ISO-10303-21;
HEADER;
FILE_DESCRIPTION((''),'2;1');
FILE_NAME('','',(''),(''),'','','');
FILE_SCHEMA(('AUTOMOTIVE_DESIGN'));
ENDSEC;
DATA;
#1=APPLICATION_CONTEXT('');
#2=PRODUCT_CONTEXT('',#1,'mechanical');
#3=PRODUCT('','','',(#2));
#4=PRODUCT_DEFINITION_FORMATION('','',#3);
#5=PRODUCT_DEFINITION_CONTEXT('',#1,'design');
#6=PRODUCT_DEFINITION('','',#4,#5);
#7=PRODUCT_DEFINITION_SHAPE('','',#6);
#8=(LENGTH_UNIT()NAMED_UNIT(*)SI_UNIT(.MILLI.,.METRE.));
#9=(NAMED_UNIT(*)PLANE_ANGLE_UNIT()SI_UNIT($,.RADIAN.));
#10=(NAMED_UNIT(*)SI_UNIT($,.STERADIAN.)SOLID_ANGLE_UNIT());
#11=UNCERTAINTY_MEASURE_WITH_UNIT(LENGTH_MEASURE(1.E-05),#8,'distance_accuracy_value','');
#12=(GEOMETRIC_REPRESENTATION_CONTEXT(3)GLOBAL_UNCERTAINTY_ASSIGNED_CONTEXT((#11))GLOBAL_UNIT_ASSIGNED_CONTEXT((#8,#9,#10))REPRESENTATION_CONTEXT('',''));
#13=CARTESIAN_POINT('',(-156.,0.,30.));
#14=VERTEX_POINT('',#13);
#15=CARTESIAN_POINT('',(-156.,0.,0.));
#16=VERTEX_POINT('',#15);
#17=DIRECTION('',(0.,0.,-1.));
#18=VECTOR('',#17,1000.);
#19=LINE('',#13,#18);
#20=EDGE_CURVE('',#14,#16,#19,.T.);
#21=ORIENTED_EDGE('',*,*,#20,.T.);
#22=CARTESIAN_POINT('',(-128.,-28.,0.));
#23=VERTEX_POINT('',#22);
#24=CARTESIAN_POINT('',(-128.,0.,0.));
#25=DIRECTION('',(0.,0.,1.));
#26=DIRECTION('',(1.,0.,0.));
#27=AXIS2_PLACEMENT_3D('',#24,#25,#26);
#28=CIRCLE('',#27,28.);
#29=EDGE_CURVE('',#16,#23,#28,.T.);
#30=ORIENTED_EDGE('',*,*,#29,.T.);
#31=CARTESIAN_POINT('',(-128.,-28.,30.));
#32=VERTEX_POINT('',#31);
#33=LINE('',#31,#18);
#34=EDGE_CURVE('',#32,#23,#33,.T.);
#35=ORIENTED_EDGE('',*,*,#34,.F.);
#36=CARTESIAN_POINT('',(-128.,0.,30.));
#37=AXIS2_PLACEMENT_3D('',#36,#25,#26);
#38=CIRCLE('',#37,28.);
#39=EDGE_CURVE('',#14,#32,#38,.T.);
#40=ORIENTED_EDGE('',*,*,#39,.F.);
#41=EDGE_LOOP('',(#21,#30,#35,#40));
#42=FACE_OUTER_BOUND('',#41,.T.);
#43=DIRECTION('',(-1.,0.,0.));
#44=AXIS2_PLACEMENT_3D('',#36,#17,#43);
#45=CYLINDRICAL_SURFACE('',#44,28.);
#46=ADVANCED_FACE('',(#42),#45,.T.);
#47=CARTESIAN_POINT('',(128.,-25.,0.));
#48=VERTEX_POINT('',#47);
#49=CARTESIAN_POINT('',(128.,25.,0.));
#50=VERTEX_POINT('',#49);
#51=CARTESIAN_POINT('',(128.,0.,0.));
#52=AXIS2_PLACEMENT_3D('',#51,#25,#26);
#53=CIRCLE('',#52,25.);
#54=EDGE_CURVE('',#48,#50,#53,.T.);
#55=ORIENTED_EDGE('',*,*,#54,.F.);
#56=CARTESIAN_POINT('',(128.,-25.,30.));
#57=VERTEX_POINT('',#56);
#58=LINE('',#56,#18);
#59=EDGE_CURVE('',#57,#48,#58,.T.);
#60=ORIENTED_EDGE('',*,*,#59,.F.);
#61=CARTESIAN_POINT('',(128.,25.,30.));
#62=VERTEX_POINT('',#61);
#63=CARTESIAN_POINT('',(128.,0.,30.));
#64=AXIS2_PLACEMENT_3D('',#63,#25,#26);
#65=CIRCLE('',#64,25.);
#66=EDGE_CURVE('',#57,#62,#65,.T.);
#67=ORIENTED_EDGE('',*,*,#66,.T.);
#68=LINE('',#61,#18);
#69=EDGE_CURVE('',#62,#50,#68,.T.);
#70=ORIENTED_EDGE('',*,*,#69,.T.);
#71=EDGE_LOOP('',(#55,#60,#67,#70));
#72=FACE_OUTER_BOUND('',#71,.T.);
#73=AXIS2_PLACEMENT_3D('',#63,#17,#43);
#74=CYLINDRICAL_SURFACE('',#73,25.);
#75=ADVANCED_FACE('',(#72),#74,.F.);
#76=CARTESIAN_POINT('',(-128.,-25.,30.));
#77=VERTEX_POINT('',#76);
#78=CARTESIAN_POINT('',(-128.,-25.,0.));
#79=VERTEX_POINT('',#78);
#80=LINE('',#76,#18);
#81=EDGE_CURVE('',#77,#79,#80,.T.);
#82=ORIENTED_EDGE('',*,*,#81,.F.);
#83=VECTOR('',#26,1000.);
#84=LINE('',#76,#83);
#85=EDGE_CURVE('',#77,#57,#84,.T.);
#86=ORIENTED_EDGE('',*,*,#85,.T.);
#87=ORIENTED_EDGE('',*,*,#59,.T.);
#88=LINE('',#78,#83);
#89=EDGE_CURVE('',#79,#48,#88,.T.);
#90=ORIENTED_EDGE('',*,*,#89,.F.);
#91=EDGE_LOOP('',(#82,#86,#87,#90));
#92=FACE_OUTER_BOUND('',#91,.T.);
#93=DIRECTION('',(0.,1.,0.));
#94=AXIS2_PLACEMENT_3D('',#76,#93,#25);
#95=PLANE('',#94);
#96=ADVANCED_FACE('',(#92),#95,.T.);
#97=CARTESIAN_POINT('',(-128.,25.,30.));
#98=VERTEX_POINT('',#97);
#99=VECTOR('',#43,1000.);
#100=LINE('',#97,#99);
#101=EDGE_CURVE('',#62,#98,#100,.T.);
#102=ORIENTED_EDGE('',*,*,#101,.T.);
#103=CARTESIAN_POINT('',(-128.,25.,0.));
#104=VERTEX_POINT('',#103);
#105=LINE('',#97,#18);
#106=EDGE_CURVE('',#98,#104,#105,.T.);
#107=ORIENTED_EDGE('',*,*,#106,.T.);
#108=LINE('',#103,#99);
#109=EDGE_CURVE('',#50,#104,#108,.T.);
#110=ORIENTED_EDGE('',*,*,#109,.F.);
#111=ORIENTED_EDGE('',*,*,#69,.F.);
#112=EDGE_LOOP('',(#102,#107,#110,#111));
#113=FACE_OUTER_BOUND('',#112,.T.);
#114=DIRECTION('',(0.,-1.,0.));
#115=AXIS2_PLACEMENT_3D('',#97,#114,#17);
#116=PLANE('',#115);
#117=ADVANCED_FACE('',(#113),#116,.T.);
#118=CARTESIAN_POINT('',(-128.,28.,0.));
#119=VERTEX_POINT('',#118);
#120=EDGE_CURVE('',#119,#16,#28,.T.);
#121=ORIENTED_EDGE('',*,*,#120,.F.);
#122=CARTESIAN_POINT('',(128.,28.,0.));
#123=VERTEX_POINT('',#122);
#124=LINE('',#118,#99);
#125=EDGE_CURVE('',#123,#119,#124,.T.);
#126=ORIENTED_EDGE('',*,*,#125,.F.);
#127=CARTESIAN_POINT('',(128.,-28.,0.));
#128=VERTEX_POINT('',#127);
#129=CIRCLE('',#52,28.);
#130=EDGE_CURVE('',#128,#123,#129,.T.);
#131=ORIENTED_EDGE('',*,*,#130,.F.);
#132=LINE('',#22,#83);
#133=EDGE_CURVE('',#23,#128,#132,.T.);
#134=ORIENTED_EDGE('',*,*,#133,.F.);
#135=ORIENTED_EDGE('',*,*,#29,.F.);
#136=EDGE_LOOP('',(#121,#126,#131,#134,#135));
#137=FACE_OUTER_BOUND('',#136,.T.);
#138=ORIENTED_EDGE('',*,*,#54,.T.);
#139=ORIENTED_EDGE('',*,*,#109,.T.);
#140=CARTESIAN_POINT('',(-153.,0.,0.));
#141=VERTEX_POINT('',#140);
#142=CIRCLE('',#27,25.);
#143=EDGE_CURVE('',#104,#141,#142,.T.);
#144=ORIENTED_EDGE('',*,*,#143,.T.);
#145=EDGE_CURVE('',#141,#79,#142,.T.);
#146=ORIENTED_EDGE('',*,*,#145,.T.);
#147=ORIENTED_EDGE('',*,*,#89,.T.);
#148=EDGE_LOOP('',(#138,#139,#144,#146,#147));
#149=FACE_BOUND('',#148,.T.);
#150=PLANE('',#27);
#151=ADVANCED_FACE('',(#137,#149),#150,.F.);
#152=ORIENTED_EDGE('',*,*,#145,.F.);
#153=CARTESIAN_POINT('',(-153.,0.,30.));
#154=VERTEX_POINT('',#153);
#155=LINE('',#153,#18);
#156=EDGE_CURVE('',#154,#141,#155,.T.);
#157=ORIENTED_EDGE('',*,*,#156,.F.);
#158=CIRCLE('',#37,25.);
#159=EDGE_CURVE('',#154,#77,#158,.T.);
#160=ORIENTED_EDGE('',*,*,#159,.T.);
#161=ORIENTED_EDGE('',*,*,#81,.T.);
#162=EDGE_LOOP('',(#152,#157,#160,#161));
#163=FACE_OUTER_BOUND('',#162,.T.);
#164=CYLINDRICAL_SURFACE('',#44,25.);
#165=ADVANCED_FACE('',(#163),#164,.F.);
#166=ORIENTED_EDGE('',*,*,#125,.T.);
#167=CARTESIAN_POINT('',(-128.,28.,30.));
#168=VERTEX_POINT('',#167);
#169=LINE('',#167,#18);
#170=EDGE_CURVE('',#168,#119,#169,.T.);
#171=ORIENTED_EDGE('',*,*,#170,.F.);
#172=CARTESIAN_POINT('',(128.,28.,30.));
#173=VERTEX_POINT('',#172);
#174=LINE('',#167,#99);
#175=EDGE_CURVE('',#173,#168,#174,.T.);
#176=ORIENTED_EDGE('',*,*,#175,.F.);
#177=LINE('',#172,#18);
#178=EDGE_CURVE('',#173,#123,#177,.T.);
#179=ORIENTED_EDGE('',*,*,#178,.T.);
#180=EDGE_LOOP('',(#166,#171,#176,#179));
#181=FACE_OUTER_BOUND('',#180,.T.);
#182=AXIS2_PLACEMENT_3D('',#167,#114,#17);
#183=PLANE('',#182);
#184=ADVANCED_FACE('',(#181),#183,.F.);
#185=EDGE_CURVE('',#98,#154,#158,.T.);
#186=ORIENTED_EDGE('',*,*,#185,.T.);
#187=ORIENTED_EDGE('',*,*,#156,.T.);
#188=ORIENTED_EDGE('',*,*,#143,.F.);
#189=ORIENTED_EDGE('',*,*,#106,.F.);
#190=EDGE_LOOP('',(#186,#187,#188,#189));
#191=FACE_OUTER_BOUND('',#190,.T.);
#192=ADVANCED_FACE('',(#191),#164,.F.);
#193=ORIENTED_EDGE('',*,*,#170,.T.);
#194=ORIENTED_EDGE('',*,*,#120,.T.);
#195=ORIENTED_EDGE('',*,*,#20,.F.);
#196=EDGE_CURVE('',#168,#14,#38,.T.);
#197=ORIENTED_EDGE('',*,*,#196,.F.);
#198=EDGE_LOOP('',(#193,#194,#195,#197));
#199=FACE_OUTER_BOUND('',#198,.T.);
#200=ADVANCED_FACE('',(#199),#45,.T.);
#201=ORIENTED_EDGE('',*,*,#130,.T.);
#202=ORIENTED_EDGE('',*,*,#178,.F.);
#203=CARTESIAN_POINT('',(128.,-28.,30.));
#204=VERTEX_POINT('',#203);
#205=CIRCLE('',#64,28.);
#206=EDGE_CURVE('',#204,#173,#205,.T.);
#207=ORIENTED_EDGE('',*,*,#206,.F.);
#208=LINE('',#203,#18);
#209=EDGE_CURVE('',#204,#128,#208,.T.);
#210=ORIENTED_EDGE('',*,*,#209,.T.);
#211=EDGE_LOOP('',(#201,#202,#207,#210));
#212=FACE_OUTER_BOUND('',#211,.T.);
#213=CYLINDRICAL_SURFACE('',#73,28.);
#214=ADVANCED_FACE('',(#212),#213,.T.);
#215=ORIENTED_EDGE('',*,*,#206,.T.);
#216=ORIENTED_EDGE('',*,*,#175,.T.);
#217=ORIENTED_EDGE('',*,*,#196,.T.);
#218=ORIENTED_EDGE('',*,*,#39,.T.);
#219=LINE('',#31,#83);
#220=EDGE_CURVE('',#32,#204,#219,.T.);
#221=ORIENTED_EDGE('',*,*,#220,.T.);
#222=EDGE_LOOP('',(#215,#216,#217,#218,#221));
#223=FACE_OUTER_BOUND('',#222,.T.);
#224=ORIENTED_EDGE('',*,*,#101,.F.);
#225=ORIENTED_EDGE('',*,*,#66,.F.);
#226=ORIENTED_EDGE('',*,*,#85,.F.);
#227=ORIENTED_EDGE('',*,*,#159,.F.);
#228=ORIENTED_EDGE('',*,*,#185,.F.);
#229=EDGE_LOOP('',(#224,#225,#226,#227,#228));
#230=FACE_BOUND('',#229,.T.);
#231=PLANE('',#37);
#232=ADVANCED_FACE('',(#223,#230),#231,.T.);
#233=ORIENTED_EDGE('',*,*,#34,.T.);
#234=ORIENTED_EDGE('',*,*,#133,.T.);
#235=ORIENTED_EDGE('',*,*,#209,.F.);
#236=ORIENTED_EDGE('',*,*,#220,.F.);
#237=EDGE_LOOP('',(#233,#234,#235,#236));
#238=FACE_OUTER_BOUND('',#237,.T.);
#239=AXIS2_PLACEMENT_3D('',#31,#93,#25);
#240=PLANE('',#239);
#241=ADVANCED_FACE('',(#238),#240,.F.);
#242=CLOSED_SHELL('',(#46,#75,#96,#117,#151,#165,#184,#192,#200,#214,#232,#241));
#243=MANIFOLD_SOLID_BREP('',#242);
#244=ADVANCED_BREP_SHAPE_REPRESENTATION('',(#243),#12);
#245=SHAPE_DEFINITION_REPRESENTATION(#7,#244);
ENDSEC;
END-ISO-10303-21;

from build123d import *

# Parameters (mm, degrees)
EXTRUDE_1_DEPTH = 30


with BuildPart() as part:
    # 草图1 → 拉伸-薄壁1 (new body)
    with BuildSketch(Plane.XY):
        with BuildLine():
            Line((128, -28), (-128, -28))
            ThreePointArc((-128, -28), (-156, 0), (-128, 28))
            Line((-128, 28), (128, 28))
            ThreePointArc((128, 28), (156, 0), (128, -28))
        make_face()
        with BuildLine():
            Line((128, -25), (-128, -25))
            ThreePointArc((-128, -25), (-153, 0), (-128, 25))
            Line((-128, 25), (128, 25))
            ThreePointArc((128, 25), (153, 0), (128, -25))
        make_face(mode=Mode.SUBTRACT)
    extrude(amount=EXTRUDE_1_DEPTH)


solid = part.part
